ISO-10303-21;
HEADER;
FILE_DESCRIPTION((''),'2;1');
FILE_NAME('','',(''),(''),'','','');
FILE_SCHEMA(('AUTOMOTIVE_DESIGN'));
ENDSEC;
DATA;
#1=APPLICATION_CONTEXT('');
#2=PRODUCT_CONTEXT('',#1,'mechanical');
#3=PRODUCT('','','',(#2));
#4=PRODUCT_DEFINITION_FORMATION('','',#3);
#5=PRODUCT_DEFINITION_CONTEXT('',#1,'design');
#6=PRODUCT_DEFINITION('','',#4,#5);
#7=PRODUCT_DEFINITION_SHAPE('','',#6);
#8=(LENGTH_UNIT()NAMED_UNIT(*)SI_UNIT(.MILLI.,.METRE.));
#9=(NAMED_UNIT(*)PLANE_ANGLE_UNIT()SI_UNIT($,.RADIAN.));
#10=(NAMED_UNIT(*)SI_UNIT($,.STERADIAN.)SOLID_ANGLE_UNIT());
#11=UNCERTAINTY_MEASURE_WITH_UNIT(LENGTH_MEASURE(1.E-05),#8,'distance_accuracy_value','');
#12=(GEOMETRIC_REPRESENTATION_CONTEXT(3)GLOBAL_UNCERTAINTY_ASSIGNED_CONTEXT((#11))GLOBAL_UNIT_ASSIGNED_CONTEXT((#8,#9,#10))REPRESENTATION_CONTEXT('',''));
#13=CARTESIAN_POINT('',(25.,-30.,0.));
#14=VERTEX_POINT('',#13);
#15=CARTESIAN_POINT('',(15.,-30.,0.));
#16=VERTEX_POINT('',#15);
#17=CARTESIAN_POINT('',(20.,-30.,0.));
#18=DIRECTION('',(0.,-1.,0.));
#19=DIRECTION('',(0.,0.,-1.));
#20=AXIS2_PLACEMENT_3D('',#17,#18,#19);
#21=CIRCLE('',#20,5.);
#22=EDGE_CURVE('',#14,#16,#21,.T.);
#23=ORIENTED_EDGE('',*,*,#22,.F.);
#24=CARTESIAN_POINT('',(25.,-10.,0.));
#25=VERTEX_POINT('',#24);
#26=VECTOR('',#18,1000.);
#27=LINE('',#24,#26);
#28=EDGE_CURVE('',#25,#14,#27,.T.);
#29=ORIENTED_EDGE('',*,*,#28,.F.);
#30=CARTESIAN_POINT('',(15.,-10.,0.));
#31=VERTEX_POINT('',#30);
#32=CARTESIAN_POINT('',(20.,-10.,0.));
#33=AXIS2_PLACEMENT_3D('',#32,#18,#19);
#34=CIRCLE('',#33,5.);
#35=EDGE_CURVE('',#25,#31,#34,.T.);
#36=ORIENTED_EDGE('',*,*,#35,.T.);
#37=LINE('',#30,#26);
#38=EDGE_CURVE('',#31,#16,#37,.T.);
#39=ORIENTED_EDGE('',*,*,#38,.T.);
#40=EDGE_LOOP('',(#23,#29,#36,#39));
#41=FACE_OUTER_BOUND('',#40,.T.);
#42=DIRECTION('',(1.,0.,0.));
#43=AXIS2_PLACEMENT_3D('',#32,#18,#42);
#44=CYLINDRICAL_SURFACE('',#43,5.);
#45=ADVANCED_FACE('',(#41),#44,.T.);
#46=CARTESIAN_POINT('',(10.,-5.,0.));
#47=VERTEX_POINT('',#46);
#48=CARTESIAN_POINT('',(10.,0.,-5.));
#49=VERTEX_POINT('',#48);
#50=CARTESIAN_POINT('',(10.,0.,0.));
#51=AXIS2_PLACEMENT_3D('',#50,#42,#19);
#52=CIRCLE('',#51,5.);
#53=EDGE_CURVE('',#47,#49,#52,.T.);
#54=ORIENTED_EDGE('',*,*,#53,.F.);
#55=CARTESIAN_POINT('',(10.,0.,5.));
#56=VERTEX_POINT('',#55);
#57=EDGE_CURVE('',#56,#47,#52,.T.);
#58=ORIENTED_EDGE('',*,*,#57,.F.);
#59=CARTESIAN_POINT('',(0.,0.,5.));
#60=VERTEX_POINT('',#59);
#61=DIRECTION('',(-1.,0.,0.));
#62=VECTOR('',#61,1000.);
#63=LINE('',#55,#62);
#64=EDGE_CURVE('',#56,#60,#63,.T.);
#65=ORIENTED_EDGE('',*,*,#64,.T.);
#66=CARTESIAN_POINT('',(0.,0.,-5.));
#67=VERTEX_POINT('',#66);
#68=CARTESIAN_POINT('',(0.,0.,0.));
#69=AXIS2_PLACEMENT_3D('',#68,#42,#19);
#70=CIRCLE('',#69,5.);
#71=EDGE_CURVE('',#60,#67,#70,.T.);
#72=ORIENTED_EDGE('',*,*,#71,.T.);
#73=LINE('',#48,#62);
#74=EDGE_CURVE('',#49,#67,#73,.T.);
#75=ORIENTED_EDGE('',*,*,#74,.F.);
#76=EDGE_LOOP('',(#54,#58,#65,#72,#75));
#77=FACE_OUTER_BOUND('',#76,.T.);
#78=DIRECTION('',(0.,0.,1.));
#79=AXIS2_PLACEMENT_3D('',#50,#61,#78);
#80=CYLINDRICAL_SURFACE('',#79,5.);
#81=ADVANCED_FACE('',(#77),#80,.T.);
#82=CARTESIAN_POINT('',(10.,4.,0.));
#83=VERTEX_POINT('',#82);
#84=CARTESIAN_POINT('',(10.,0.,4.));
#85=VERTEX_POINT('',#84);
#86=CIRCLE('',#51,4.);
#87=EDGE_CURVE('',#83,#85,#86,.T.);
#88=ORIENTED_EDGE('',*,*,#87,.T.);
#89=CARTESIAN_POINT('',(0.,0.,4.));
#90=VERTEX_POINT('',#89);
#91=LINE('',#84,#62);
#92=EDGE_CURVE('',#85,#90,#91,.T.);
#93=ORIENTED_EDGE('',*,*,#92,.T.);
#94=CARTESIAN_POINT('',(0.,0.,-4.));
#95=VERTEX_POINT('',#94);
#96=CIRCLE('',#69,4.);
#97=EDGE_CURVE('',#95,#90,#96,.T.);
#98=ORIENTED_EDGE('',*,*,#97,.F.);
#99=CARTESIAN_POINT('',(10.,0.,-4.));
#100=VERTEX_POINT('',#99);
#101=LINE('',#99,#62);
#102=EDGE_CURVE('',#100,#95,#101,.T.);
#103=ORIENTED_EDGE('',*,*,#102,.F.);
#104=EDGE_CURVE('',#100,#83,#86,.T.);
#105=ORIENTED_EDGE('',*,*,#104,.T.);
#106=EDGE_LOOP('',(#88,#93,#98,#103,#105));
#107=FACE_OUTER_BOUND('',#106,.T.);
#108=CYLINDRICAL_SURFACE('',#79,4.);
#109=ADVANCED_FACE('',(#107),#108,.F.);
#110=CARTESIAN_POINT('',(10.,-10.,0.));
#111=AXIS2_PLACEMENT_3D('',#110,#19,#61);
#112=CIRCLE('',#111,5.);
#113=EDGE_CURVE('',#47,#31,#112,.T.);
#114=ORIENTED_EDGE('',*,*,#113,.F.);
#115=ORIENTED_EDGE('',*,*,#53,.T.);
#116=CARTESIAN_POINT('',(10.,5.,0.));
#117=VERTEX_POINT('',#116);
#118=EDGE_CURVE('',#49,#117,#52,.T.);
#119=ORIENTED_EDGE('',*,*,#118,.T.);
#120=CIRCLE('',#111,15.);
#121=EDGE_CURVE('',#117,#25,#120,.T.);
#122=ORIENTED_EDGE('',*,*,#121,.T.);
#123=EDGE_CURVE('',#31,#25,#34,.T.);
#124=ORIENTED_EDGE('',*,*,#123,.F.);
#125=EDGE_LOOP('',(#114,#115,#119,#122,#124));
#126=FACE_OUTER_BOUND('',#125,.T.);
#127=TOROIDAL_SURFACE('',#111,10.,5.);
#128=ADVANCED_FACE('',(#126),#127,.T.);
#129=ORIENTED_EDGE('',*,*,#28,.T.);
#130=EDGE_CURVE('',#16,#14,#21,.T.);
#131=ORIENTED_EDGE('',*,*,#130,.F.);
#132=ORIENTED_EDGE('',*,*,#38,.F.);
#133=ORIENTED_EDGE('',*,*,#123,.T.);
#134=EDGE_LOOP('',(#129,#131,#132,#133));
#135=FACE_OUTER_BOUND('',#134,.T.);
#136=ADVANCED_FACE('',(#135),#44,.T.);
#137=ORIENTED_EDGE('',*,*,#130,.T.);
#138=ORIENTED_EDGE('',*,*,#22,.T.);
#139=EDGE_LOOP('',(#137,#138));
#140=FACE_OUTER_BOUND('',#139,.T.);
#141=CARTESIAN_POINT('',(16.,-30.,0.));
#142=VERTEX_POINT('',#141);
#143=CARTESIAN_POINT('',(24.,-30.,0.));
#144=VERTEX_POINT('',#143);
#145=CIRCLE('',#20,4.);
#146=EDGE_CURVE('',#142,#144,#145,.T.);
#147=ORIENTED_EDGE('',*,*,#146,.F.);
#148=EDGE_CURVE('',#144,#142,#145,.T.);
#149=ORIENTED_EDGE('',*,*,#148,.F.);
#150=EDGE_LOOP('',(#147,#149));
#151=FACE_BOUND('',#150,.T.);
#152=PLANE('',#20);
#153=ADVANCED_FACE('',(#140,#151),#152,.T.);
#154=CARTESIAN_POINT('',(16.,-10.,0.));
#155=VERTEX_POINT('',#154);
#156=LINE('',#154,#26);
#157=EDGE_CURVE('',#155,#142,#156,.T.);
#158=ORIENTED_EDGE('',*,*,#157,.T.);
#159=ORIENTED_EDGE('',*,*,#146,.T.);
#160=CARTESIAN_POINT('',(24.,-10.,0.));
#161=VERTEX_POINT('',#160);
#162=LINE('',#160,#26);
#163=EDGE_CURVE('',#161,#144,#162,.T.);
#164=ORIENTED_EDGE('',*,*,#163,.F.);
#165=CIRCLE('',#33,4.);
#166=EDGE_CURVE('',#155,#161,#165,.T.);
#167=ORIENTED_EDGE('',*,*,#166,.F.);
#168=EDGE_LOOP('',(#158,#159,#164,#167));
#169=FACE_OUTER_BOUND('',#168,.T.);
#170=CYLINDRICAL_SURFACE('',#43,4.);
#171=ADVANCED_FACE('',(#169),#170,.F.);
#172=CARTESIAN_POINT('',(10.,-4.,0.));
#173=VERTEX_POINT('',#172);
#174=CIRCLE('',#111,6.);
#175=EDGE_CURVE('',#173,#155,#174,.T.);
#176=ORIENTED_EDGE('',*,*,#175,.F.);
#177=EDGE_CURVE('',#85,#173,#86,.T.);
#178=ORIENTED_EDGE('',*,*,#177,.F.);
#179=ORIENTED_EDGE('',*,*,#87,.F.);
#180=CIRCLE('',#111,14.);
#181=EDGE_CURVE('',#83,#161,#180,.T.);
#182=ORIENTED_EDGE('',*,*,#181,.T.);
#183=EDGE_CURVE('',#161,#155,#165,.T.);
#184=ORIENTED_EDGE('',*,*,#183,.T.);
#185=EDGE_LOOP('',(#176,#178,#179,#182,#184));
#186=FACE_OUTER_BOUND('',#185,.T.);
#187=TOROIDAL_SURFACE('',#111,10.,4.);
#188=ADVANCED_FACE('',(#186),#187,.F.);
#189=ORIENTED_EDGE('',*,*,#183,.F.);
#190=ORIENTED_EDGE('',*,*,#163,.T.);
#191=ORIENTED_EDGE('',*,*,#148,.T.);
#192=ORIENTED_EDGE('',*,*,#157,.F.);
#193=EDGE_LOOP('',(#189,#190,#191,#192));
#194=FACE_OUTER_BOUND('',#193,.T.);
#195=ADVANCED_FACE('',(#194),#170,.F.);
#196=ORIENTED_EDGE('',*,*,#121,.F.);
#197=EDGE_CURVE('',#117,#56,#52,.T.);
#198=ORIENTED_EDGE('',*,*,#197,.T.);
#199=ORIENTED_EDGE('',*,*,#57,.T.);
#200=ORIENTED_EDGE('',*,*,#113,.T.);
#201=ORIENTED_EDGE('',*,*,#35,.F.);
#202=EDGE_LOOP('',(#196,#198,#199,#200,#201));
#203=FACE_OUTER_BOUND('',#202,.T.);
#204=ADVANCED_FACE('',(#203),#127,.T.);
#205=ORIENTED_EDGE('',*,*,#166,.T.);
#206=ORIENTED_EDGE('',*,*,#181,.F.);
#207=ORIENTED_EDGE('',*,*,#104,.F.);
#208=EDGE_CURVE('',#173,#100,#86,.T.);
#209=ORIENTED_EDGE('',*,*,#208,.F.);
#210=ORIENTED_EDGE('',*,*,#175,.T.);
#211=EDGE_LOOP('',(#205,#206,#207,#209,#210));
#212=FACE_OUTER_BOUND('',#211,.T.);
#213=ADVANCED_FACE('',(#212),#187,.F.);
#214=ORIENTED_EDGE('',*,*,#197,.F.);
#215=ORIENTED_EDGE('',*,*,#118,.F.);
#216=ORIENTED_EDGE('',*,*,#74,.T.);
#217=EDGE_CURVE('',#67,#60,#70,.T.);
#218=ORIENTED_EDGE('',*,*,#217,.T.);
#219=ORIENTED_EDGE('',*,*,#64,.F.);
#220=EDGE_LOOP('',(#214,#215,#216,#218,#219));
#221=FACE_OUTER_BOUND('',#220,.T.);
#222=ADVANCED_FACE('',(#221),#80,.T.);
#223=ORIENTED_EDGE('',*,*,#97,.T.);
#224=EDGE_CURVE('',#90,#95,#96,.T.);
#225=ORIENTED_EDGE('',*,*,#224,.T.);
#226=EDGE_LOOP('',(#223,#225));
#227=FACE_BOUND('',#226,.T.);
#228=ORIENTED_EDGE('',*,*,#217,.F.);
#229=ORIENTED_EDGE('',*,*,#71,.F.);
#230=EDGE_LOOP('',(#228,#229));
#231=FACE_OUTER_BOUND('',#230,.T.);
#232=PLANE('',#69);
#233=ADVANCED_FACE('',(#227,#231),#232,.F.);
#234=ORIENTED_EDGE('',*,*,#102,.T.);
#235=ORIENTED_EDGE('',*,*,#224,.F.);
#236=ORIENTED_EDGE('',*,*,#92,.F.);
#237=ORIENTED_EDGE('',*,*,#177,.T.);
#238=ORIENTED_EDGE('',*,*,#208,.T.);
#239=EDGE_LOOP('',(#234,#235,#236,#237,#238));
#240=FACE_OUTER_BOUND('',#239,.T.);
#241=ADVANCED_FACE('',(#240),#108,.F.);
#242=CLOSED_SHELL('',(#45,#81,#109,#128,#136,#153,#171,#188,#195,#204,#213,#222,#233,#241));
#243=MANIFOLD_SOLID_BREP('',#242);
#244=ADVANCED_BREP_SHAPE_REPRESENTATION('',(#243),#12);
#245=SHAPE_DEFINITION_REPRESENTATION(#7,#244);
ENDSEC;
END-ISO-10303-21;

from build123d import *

# Parameters (mm, degrees)
SKETCH2_R   = 5
SKETCH2_R_2 = 4


with BuildPart() as part:
    # Sweep1: sweep along a path in Sketch1
    with BuildLine(Plane.XY) as sweep1_path:
        Line((0, 0), (10, 0))
        ThreePointArc((10, 0), (17.071067812, -2.928932188), (20, -10))
        Line((20, -10), (20, -30))
    # Sketch2 → Sweep1 (sweep)
    with BuildSketch(Plane(origin=(0, 0, 0), x_dir=(0, 0, -1), z_dir=(1, 0, 0))):
        Circle(SKETCH2_R)
        Circle(SKETCH2_R_2, mode=Mode.SUBTRACT)
    sweep(path=sweep1_path.line)


solid = part.part
